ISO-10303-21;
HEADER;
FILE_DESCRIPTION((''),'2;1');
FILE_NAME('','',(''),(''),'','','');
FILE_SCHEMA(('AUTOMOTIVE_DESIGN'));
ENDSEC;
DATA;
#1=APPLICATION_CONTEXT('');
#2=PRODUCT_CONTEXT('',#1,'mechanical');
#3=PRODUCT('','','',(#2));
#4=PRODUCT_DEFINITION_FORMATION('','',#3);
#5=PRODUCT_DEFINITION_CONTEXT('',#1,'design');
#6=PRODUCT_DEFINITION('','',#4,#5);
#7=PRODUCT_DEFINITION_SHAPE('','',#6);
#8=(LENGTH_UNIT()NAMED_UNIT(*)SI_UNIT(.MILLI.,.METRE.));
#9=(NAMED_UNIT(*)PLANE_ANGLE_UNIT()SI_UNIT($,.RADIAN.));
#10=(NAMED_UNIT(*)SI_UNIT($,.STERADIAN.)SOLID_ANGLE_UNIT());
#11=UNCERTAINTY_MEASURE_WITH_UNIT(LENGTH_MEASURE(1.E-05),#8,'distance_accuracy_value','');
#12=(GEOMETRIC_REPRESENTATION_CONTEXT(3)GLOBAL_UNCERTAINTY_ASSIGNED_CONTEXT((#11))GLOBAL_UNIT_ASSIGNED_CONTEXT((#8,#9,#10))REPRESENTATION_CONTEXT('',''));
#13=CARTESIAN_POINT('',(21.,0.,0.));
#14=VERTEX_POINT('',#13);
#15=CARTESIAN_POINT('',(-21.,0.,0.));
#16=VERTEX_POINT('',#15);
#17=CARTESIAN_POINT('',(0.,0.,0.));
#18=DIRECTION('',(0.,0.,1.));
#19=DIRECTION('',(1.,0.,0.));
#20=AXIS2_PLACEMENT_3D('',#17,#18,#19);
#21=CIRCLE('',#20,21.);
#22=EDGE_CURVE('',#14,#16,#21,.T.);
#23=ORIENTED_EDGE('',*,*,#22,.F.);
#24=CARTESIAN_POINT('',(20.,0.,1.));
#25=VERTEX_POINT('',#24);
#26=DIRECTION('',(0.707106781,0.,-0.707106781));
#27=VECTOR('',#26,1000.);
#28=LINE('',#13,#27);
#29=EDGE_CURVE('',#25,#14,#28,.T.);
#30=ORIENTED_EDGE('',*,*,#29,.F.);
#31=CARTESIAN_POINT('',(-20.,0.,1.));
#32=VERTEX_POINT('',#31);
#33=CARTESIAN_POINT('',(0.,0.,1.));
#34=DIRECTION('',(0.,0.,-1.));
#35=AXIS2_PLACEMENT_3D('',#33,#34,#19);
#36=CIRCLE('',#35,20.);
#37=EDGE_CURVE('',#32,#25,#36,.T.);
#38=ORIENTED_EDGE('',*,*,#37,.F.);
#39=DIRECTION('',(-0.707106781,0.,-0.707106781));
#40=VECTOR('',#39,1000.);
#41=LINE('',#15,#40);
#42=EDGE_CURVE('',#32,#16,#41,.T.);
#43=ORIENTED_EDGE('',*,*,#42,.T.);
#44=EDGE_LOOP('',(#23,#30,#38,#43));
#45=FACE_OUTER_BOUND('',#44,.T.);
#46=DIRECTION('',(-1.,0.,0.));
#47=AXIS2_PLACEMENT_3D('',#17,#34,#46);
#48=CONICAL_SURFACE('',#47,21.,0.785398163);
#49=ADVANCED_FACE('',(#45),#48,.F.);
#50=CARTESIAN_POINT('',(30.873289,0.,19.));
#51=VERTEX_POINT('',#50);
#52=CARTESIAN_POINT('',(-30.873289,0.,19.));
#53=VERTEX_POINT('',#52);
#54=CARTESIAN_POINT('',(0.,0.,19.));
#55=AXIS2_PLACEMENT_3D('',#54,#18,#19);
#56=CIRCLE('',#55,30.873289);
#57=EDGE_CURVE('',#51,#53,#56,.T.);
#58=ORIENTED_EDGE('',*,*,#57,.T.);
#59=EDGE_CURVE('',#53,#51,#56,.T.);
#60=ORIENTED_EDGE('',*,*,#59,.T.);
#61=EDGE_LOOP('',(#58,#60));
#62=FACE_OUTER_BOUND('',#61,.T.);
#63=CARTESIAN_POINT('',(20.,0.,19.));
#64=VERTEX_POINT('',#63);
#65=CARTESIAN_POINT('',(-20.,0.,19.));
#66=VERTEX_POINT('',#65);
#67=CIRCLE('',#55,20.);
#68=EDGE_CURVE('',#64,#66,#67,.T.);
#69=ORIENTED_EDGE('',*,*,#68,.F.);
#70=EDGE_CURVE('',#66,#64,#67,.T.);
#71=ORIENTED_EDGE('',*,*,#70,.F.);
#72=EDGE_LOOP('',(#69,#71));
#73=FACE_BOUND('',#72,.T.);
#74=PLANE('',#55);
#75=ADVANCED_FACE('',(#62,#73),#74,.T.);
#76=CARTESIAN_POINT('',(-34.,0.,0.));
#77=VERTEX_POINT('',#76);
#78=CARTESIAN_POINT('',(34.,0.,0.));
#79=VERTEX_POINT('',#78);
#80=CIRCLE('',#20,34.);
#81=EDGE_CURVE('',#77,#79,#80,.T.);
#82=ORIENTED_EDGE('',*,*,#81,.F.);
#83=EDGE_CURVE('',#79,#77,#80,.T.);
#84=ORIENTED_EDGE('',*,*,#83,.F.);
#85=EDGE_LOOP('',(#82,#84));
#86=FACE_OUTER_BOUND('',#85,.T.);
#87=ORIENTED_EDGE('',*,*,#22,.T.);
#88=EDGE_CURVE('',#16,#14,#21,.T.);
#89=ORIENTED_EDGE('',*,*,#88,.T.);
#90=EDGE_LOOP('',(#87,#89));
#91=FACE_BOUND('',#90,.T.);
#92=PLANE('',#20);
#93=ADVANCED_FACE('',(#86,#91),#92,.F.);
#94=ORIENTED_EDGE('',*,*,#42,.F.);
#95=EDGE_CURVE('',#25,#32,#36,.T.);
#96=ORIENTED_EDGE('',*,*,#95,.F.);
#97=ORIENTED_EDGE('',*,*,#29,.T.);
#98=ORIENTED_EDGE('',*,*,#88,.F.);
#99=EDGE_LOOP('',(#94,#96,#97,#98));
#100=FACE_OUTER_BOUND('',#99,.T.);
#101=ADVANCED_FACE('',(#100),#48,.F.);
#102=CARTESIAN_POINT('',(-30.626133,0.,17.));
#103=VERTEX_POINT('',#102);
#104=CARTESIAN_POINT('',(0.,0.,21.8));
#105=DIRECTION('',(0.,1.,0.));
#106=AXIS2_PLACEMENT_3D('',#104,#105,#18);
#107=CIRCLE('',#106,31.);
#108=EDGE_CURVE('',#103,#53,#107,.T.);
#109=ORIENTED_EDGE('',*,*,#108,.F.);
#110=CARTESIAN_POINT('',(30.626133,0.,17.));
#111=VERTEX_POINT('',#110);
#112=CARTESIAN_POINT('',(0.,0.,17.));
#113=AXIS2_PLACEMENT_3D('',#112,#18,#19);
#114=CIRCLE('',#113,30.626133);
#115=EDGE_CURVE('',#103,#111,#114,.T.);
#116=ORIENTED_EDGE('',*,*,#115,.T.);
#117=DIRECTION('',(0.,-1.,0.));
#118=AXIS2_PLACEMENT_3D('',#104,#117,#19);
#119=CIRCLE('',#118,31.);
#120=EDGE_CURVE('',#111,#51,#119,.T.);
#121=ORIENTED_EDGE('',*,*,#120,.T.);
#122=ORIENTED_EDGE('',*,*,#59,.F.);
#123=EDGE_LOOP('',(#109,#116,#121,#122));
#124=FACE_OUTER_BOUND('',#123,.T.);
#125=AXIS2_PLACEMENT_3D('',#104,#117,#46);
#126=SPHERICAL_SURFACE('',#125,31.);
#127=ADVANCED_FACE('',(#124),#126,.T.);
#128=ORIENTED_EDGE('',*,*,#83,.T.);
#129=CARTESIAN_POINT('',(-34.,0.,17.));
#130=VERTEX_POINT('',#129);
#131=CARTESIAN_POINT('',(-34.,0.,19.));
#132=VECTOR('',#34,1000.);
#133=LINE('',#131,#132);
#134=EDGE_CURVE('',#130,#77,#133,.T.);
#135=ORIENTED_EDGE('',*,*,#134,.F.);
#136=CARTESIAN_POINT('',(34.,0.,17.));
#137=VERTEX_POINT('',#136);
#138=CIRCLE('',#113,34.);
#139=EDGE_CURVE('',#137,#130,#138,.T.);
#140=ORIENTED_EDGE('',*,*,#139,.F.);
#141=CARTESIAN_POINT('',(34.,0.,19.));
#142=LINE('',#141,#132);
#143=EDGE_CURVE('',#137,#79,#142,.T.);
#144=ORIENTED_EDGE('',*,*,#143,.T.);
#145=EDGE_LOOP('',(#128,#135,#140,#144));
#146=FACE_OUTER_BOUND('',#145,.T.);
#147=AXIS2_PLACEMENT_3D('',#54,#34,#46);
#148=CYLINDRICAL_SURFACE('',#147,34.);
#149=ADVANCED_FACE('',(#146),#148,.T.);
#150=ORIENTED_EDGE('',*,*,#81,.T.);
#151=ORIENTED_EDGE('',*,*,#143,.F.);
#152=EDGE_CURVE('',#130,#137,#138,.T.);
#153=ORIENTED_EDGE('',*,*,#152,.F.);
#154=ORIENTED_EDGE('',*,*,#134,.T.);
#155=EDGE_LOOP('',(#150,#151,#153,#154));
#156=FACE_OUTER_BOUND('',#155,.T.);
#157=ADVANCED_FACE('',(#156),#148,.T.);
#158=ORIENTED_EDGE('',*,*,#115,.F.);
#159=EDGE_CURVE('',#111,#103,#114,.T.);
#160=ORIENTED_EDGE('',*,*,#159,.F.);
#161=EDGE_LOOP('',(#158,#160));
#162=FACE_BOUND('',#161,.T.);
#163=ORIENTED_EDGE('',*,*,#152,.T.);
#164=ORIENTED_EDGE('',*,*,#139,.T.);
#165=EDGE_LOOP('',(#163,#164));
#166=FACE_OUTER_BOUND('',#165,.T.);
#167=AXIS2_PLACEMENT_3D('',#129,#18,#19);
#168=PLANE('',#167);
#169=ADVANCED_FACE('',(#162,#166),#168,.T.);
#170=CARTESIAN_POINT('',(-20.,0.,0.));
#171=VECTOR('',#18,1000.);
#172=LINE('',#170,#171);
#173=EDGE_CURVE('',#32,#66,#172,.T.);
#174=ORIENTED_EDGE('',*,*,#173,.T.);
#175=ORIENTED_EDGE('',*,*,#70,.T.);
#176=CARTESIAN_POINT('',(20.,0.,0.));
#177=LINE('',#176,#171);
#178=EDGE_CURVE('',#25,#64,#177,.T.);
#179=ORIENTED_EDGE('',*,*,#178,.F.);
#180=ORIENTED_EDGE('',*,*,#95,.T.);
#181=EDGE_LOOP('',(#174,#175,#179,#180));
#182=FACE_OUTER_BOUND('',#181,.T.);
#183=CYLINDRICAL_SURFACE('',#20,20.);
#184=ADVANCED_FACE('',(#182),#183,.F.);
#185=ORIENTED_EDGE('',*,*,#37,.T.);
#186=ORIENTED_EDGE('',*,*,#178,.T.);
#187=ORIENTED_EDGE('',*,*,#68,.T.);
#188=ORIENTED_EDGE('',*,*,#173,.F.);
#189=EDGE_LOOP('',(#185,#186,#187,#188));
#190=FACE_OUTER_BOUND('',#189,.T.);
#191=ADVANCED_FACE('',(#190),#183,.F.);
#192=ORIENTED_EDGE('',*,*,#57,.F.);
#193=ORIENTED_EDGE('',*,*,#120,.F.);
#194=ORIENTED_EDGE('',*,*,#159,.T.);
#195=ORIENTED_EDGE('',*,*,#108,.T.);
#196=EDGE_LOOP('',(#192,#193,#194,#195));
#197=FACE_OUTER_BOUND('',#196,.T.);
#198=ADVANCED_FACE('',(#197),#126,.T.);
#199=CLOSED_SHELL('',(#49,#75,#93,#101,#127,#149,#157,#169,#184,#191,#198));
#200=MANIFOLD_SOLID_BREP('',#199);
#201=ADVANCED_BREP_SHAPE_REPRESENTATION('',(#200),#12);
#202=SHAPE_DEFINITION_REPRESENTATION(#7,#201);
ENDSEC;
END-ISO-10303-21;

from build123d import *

# Parameters (mm, degrees)
SKETCH_1_R          = 34
EXTRUDE_1_DEPTH     = 19
SKETCH_3_R          = 20
CUT_EXTRUDE_1_DEPTH = 52.701063819
CHAMFER_1_SIZE      = 1


with BuildPart() as part:
    # 草图1 → 凸台-拉伸1 (new body)
    with BuildSketch(Plane.XY):
        Circle(SKETCH_1_R)
    extrude(amount=EXTRUDE_1_DEPTH)

    # 草图2 → 切除-旋转1 (revolve, cut)
    with BuildSketch(Plane(origin=(0, 0, 0), x_dir=(1, 0, 0), z_dir=(0, 1, 0)), mode=Mode.PRIVATE) as cut_revolve_1_sk:
        with BuildLine():
            Line((-34, -17), (-30.626132632, -17))
            ThreePointArc((-30.626132632, -17), (-30.765967048, -17.997991107), (-30.873289426, -19))
            Line((-30.873289426, -19), (-34, -19))
            Line((-34, -19), (-34, -17))
        make_face()
    revolve(cut_revolve_1_sk.sketch.rotate(Axis((0, 0, 19), (0, 0, -1)), 180), axis=Axis((0, 0, 19), (0, 0, -1)), mode=Mode.SUBTRACT)

    # 草图3 → 切除-拉伸1 (cut, through all)
    with BuildSketch(Plane.XY.offset(19)):
        Circle(SKETCH_3_R)
    extrude(amount=-CUT_EXTRUDE_1_DEPTH, mode=Mode.SUBTRACT)

    # 倒角1
    chamfer_1_edges = [part.edges().sort_by_distance(p)[0] for p in [
        (-20, 0, 0),
    ]]
    chamfer(chamfer_1_edges, length=CHAMFER_1_SIZE)


solid = part.part
